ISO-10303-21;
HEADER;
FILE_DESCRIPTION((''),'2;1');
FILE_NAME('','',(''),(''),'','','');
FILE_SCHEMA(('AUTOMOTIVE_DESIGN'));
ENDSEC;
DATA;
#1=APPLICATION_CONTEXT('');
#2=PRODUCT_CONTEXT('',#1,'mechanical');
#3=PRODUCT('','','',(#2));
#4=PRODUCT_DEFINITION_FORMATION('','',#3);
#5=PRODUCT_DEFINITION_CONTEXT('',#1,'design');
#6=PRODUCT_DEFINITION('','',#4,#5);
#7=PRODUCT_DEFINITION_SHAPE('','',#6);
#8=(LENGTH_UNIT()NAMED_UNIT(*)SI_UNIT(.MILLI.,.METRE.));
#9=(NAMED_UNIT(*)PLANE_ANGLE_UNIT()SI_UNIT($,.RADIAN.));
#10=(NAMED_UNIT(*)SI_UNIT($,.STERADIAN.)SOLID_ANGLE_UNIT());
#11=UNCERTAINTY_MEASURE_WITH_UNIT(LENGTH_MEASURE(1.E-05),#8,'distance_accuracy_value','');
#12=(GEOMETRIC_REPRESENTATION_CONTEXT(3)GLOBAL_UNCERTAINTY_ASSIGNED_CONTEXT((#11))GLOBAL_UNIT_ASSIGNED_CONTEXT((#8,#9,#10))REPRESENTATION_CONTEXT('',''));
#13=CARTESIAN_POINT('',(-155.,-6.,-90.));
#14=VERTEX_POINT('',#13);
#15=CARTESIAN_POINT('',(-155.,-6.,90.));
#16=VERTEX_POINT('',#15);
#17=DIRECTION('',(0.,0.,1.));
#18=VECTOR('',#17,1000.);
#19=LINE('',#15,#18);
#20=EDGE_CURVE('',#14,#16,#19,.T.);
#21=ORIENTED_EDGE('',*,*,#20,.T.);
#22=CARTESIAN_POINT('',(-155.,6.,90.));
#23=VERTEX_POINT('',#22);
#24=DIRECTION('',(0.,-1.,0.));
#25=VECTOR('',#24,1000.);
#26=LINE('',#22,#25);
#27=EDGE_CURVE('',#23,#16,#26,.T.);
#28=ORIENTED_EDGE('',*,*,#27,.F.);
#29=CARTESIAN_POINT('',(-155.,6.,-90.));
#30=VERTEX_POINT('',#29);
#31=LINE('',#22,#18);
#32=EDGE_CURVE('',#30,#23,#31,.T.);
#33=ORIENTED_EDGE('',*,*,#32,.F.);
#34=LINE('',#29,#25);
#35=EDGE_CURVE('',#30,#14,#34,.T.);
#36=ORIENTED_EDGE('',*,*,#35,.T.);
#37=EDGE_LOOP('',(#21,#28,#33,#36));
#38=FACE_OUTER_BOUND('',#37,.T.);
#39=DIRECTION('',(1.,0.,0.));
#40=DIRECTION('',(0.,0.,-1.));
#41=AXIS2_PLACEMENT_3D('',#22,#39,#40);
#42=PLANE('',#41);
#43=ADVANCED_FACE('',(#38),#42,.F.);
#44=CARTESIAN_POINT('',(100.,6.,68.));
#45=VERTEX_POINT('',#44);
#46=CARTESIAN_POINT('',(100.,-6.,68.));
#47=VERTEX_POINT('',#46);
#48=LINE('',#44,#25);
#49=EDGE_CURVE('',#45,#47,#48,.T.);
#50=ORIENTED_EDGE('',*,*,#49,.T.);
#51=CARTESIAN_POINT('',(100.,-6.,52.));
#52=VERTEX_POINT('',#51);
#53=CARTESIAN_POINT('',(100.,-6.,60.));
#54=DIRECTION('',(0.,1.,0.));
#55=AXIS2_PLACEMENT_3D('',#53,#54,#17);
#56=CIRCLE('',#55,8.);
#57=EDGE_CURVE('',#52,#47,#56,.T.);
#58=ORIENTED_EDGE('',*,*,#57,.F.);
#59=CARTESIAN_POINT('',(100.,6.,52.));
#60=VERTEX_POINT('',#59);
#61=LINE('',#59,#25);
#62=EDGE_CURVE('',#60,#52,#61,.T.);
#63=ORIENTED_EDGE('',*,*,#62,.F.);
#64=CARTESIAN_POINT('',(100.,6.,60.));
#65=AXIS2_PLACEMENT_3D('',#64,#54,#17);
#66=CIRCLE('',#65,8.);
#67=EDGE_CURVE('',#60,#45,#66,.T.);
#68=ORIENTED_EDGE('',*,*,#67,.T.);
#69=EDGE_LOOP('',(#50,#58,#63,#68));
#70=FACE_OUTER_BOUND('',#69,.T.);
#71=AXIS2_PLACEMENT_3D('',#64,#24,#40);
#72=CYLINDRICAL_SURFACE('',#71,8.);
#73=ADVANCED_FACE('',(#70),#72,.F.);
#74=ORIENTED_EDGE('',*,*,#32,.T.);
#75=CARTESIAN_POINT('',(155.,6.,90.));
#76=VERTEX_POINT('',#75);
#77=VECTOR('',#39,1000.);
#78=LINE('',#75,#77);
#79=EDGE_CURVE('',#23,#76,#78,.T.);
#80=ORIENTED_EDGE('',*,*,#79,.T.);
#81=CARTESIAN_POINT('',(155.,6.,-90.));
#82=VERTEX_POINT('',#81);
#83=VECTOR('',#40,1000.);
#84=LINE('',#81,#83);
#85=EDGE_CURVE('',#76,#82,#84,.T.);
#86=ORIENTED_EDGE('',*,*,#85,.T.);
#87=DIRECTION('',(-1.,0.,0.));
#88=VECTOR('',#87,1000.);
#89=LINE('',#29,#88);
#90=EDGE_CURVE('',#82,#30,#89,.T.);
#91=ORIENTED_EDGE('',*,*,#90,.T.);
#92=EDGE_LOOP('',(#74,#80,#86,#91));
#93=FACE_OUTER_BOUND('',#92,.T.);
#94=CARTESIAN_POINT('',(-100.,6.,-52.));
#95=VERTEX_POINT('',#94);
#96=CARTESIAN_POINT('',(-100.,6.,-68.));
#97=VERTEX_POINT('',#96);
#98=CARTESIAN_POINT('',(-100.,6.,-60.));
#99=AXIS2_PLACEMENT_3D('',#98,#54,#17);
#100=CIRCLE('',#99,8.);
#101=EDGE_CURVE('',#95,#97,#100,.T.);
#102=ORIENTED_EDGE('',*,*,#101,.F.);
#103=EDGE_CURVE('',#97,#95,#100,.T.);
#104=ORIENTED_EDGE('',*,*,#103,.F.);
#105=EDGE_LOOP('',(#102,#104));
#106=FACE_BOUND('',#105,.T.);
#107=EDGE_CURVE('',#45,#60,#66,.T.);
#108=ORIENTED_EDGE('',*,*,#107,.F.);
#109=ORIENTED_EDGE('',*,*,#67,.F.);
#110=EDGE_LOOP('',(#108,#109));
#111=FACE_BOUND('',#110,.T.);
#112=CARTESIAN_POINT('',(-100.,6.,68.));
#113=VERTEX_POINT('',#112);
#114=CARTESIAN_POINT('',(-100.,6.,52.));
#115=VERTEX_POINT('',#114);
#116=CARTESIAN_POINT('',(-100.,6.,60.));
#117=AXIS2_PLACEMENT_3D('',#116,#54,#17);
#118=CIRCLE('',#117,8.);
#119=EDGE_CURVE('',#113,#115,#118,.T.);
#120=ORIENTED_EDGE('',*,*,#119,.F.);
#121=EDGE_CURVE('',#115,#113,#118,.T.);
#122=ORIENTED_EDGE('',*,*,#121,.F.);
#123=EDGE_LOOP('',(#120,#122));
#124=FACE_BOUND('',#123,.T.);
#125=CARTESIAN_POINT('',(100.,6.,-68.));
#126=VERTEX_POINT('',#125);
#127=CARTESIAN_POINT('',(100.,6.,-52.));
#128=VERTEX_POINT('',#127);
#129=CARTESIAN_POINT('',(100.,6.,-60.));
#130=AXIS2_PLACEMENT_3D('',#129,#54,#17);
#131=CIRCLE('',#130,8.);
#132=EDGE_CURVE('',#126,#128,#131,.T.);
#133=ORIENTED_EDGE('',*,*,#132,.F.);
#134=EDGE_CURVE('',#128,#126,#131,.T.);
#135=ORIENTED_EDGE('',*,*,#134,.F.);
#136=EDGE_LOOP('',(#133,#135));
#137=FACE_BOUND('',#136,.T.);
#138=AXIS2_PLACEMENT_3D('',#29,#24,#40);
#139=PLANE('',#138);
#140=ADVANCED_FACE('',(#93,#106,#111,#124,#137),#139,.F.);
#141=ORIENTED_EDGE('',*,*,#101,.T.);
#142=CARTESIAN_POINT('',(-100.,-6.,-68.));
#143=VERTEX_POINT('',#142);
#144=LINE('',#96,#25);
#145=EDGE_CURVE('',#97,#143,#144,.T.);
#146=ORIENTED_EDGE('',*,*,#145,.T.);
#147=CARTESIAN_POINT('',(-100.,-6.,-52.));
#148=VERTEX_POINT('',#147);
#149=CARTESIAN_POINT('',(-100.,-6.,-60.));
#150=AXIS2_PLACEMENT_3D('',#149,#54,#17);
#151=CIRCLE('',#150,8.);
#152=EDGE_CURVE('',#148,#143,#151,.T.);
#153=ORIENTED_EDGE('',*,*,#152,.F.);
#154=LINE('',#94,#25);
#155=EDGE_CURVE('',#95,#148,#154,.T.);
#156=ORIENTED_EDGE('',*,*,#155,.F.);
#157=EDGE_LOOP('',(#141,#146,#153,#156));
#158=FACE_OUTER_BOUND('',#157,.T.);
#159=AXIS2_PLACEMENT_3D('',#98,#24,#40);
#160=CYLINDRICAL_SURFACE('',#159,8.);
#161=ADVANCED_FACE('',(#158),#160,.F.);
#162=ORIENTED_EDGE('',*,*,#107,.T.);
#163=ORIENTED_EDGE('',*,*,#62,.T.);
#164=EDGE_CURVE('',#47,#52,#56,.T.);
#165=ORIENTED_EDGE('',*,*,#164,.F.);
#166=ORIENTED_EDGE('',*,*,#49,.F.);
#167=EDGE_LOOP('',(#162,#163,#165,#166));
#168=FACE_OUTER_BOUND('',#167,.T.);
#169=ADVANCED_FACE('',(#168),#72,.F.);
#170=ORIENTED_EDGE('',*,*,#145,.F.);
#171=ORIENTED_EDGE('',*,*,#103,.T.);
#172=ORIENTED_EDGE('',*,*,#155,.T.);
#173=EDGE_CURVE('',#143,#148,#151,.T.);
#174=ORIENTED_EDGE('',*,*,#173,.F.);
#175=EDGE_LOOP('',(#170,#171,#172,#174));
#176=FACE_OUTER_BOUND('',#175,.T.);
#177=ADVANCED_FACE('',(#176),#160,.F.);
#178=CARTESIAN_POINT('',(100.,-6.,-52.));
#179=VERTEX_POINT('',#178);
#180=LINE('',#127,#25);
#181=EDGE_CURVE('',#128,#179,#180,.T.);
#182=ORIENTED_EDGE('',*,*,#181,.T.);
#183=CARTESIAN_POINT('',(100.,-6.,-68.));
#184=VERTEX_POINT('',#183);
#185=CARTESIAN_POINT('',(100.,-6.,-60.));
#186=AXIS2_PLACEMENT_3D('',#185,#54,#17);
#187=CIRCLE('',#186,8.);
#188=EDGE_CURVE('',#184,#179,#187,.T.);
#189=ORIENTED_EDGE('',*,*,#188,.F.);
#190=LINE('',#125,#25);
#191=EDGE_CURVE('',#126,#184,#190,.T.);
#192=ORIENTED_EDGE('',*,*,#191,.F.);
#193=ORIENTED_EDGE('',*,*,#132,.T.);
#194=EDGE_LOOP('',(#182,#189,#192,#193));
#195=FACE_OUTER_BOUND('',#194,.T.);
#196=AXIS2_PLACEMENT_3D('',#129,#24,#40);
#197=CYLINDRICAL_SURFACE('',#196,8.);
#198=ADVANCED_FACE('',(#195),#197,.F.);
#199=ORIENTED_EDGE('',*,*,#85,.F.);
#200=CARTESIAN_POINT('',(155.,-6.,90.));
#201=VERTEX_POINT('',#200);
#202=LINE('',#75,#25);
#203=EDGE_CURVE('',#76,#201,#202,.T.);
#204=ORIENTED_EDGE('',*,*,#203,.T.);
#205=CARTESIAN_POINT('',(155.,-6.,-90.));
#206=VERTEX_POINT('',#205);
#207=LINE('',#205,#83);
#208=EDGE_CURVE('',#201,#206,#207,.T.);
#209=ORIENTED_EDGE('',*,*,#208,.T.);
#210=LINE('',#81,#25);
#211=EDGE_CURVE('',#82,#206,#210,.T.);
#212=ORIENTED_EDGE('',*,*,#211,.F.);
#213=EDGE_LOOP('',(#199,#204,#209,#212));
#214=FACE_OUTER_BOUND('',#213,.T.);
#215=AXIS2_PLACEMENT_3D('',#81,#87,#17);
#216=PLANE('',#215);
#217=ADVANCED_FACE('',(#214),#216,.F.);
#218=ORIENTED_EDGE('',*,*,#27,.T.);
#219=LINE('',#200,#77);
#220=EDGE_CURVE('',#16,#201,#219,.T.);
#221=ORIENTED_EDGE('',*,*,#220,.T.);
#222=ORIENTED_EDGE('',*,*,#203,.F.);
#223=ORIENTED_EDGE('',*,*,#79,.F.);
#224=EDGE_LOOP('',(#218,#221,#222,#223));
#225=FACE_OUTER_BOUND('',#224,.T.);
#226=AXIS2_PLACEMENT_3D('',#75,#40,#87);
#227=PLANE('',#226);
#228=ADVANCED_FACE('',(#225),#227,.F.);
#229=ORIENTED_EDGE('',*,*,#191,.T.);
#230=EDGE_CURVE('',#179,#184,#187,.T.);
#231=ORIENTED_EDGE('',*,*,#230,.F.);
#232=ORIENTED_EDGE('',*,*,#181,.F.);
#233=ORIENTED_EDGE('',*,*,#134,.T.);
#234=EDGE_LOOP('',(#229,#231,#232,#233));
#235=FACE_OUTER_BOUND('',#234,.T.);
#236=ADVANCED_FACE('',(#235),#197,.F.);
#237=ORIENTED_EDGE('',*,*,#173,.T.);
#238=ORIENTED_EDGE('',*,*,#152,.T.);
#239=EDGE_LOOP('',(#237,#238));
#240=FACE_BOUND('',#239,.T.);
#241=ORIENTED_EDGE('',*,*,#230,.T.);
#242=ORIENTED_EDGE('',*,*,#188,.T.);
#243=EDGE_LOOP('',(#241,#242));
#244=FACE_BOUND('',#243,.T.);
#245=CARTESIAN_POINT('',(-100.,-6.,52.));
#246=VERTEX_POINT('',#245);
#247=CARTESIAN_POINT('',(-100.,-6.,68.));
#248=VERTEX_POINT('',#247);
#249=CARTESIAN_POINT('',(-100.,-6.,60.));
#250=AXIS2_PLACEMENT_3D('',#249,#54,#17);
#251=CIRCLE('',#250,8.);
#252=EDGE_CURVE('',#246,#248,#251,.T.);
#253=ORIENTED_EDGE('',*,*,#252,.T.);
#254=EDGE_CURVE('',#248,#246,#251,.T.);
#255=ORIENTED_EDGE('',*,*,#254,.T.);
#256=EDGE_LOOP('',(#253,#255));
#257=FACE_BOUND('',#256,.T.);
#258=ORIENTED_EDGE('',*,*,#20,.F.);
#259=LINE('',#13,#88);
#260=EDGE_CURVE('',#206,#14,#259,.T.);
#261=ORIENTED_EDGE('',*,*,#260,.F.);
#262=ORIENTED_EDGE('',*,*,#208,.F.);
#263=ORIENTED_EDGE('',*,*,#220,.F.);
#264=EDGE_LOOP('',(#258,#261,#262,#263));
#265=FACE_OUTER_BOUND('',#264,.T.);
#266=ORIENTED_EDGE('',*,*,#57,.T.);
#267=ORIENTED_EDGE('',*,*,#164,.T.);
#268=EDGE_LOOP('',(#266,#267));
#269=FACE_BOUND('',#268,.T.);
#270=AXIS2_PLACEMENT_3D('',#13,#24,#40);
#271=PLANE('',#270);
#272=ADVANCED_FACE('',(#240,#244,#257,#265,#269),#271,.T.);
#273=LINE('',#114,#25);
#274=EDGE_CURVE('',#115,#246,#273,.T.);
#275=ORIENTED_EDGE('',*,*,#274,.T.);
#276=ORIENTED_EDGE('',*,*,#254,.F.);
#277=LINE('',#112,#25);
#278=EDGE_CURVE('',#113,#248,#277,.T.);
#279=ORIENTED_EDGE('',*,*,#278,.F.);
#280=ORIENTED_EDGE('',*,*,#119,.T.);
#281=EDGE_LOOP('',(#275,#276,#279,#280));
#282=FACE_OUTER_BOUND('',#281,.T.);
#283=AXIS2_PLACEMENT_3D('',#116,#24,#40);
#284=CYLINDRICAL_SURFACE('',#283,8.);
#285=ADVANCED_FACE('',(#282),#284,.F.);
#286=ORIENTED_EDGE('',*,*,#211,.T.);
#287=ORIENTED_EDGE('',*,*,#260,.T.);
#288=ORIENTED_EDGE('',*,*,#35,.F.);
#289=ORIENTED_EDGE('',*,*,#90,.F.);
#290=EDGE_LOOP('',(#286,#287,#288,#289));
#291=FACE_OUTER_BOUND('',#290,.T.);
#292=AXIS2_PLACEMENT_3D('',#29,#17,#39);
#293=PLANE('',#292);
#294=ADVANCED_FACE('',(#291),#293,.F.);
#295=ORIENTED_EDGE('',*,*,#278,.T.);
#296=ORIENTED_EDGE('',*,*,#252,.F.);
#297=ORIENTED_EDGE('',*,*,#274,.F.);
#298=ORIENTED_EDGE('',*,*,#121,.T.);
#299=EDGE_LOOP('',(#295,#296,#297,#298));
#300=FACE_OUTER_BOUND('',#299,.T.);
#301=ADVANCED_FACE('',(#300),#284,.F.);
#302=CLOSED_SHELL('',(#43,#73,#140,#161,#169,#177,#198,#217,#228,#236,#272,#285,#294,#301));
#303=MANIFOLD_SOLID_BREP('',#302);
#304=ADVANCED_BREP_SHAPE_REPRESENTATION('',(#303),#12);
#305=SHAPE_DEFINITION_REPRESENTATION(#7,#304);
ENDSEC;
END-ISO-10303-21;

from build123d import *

# Parameters (mm, degrees)
SKETCH1_W      = 310
SKETCH1_H      = 180
SKETCH1_R      = 8
EXTRUDE1_DEPTH = 6


with BuildPart() as part:
    # Sketch1 → Extrude1 (new, symmetric)
    with BuildSketch(Plane(origin=(0, 0, 0), x_dir=(1, 0, 0), z_dir=(0, 1, 0))):
        Rectangle(SKETCH1_W, SKETCH1_H)
        with Locations(Location((100, -60, 0), (0, 0, 270))):
            Circle(SKETCH1_R, mode=Mode.SUBTRACT)
        with Locations(Location((-100, -60, 0), (0, 0, 270))):
            Circle(SKETCH1_R, mode=Mode.SUBTRACT)
        with Locations(Location((-100, 60, 0), (0, 0, 270))):
            Circle(SKETCH1_R, mode=Mode.SUBTRACT)
        with Locations(Location((100, 60, 0), (0, 0, 270))):
            Circle(SKETCH1_R, mode=Mode.SUBTRACT)
    extrude(amount=EXTRUDE1_DEPTH, both=True)


solid = part.part
